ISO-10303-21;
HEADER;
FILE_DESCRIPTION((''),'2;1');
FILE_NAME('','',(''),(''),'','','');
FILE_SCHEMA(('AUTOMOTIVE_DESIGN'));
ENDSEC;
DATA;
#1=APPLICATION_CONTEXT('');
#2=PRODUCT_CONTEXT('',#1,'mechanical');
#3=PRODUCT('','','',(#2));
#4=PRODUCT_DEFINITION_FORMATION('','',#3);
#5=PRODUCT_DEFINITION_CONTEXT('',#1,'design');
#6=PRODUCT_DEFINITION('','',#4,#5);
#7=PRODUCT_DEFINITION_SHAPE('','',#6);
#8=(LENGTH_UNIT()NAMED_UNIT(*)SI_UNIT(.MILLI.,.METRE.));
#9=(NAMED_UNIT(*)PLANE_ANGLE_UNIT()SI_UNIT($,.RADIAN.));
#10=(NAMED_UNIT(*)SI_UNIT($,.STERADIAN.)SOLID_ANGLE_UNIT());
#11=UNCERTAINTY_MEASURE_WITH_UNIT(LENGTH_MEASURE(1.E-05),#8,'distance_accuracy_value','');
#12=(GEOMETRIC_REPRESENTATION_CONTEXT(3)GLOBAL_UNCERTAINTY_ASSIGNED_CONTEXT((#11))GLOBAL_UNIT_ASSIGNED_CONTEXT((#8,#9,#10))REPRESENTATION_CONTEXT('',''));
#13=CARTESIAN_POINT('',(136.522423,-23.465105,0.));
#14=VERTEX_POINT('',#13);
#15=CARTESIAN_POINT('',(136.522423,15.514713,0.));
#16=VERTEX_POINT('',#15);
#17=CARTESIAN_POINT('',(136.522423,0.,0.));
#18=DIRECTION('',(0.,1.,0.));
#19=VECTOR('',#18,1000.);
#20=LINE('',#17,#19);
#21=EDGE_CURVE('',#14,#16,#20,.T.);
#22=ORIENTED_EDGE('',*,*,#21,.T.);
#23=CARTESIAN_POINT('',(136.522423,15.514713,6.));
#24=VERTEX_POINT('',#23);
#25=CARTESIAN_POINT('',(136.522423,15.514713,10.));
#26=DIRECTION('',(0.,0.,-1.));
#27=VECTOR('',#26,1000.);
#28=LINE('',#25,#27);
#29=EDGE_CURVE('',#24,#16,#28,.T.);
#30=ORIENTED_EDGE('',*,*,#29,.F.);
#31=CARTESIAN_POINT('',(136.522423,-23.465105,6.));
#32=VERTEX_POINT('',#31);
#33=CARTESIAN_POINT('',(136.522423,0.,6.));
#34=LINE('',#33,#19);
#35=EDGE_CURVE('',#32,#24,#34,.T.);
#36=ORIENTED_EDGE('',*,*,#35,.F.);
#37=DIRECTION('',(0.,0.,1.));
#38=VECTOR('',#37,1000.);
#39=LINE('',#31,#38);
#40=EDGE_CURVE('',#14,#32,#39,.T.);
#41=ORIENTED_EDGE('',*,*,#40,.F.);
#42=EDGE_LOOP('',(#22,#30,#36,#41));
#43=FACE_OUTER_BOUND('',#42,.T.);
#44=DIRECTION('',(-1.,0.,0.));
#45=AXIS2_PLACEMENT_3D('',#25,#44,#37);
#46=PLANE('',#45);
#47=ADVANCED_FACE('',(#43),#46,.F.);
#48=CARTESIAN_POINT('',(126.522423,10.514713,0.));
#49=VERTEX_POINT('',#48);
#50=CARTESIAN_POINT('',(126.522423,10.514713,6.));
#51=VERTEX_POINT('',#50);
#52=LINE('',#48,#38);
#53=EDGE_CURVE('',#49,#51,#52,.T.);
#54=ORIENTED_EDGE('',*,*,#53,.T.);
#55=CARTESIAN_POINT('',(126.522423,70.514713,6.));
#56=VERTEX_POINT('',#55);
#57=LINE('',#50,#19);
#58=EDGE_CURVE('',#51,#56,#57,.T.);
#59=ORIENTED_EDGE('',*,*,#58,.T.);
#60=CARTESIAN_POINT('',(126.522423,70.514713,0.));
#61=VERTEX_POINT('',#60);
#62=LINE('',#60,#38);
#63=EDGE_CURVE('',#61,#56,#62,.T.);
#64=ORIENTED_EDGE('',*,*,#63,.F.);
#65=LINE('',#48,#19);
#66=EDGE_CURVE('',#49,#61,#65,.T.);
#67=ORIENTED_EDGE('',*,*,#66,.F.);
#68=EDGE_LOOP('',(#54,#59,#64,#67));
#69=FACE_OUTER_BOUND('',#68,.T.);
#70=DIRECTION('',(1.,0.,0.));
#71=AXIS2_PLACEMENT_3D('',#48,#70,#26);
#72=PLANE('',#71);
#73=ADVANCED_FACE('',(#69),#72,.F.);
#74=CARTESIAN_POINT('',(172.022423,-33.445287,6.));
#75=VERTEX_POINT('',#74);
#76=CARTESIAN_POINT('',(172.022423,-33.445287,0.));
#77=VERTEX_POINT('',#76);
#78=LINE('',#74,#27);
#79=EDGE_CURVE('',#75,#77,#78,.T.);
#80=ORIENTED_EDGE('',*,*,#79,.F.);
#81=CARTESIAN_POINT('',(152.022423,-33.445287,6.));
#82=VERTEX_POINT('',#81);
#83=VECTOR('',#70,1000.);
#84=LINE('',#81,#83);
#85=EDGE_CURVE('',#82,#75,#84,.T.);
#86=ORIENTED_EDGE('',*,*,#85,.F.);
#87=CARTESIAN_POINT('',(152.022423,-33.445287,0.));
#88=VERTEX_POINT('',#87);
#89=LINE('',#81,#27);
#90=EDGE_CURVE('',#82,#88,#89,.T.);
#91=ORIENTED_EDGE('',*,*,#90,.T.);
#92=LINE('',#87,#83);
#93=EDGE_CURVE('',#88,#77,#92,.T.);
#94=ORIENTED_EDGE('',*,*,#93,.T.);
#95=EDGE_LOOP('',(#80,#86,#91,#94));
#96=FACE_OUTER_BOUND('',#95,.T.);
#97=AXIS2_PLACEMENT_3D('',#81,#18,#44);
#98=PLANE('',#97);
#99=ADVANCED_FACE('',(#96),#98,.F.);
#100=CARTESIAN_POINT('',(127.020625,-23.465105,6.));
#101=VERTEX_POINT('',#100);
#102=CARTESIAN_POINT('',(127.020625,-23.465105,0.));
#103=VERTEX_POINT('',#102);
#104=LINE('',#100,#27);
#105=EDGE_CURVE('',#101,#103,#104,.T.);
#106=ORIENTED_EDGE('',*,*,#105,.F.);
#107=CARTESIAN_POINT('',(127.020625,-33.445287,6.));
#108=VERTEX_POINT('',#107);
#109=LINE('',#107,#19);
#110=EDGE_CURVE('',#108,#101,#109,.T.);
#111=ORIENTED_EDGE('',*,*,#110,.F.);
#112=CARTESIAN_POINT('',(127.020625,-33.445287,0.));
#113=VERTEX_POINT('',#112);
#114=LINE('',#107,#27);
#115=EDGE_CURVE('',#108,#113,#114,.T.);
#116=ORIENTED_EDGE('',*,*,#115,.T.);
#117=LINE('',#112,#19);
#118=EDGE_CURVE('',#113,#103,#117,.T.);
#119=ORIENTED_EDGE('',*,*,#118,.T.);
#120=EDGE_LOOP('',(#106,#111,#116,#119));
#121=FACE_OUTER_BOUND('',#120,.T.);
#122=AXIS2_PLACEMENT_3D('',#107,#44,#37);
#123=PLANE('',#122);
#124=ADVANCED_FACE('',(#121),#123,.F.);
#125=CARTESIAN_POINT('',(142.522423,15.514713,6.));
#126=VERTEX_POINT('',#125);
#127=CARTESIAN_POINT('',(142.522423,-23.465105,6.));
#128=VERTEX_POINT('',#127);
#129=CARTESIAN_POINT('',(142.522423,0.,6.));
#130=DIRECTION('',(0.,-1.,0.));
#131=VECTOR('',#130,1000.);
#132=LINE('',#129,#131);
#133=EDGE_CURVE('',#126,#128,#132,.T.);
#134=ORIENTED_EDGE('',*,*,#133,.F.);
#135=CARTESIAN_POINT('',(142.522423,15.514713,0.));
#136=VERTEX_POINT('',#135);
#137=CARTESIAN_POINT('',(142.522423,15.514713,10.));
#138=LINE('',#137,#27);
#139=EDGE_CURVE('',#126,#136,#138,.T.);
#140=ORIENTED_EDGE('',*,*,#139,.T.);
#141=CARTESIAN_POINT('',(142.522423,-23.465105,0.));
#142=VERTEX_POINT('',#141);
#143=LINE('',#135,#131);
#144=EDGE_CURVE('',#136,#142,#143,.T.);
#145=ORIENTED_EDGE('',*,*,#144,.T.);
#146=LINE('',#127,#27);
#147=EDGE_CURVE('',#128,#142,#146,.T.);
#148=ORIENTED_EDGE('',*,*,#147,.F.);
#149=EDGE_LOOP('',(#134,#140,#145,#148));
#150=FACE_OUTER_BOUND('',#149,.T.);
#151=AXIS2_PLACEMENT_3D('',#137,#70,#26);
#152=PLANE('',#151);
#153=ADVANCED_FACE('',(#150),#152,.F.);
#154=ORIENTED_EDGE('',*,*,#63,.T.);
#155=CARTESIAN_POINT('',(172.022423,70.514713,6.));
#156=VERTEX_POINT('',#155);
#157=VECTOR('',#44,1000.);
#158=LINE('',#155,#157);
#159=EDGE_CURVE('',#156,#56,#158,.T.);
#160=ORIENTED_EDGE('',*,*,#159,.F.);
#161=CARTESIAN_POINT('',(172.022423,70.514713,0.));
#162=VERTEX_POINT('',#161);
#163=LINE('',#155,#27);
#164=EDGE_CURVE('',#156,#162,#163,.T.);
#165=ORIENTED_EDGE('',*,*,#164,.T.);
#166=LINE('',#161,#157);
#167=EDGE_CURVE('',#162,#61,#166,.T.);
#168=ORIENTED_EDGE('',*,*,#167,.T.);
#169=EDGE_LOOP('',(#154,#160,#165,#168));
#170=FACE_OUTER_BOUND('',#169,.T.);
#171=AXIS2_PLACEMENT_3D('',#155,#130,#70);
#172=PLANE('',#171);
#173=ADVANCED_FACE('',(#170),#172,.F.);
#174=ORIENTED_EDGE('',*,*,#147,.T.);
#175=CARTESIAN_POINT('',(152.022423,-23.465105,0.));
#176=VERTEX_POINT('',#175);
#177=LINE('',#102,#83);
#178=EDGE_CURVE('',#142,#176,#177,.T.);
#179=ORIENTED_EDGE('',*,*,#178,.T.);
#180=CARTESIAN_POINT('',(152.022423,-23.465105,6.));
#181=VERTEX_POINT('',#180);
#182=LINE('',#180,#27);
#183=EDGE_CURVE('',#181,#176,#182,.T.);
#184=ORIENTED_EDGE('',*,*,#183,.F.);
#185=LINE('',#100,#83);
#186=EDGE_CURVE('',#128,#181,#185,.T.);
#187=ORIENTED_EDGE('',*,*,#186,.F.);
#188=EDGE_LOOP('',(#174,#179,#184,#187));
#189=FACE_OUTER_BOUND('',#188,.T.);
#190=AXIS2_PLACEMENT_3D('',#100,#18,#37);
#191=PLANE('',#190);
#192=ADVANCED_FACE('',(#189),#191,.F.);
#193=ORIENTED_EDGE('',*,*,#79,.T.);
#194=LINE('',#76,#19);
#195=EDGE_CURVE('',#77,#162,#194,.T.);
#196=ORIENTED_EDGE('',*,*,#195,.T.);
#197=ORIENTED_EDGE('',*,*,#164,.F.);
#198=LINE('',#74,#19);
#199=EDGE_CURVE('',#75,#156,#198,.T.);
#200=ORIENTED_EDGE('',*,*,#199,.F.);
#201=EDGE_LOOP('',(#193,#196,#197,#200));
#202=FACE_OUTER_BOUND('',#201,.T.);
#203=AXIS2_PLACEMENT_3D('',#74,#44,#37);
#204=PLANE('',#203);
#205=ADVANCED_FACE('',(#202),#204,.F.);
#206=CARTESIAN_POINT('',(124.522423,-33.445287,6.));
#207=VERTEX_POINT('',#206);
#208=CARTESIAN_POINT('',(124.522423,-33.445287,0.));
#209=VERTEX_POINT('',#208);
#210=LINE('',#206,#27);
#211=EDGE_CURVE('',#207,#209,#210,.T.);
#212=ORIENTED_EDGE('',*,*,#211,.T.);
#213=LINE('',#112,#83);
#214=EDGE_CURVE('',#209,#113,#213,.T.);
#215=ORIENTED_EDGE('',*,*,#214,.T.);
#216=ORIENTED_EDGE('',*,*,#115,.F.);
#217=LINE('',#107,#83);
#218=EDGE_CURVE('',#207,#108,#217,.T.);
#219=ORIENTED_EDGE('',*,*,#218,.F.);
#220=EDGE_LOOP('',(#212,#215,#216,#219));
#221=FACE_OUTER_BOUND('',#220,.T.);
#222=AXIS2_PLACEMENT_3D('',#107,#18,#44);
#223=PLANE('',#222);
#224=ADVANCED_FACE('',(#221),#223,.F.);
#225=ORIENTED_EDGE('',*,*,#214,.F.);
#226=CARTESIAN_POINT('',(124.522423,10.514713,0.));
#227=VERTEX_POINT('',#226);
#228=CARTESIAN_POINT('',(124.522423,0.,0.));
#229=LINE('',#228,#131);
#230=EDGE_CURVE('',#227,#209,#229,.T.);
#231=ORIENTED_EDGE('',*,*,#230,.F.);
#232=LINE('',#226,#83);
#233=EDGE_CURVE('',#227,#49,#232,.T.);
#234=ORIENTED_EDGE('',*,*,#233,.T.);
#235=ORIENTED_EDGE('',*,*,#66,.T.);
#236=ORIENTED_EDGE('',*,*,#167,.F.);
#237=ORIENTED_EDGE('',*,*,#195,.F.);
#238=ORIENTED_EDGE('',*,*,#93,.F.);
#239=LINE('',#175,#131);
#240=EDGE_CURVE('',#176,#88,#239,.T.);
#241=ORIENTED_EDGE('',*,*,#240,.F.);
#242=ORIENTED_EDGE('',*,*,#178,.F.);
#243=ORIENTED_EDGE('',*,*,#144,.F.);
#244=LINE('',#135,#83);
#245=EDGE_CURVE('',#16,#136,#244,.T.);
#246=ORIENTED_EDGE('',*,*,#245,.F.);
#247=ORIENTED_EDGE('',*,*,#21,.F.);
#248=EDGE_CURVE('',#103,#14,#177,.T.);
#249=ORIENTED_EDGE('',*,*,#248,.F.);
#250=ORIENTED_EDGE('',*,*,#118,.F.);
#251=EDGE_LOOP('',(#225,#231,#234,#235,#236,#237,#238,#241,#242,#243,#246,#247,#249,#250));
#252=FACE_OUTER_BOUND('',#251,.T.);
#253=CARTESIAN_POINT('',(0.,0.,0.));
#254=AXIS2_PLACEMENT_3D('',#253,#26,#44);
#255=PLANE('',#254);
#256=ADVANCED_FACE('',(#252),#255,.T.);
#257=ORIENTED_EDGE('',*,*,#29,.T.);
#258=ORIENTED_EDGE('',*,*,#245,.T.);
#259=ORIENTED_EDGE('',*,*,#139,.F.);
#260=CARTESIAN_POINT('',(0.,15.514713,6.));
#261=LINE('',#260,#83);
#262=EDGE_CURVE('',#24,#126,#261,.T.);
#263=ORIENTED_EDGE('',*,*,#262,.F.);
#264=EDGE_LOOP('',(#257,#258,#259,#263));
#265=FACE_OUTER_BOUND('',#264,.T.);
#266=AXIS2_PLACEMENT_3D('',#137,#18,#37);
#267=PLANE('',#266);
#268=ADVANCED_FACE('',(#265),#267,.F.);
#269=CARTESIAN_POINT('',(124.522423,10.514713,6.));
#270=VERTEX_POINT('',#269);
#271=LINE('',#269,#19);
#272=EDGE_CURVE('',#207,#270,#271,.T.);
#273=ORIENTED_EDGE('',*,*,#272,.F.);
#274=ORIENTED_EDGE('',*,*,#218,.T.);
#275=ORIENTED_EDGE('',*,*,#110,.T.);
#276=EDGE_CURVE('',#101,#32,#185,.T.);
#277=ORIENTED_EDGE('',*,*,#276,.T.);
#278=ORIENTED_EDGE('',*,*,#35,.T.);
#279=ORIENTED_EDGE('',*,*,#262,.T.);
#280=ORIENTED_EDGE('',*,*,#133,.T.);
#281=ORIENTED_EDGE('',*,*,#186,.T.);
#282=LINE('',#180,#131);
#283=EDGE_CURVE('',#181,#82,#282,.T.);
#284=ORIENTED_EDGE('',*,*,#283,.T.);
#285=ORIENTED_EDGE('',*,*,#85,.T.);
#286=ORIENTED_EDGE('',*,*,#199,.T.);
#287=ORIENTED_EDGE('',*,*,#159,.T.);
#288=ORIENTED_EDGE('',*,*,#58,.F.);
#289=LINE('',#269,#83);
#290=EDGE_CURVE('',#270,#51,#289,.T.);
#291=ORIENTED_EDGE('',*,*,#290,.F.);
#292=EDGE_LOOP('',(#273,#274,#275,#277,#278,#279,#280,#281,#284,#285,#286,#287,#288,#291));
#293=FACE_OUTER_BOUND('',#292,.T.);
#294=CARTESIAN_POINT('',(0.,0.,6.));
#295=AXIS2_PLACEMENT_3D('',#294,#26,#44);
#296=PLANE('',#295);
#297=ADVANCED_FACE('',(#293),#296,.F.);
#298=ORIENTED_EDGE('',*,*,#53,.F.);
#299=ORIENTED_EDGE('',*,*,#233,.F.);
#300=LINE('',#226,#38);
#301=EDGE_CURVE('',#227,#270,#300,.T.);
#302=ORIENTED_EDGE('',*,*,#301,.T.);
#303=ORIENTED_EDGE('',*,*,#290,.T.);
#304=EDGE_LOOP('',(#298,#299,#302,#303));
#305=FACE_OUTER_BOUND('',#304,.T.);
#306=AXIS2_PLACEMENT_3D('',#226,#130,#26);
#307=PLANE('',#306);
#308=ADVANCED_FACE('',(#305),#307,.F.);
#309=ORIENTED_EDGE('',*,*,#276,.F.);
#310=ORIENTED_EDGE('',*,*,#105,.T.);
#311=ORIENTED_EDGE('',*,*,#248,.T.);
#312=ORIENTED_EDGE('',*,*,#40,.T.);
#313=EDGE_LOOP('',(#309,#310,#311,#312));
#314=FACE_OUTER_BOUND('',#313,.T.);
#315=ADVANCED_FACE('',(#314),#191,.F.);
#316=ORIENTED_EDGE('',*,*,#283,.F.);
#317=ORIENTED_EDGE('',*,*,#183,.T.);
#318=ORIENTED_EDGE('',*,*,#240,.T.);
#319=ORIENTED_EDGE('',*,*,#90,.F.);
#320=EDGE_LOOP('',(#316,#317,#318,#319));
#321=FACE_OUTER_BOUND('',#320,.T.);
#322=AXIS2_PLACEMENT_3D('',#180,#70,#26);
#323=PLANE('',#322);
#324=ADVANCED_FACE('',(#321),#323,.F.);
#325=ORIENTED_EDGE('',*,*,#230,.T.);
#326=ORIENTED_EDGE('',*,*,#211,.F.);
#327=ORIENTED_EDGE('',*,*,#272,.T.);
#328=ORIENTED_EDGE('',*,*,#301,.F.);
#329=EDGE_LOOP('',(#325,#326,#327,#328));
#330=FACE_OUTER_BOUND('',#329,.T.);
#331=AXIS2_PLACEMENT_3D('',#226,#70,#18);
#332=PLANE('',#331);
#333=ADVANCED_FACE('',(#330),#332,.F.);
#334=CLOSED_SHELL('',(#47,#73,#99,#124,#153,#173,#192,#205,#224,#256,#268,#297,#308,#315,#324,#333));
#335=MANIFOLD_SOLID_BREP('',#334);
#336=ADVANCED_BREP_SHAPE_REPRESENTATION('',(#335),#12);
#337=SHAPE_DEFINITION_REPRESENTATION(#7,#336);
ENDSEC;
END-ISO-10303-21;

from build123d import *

# Parameters (mm, degrees)
BOSS_EXTRUDE1_DEPTH = 6
SKETCH3_W           = 6
SKETCH3_H           = 60
CUT_EXTRUDE1_DEPTH  = 10
CUT_EXTRUDE2_DEPTH  = 187.01085661


with BuildPart() as part:
    # Sketch1 → Boss-Extrude1 (new body)
    with BuildSketch(Plane.XY):
        Polygon((127.020625139, -33.445286794), (107.020625139, -33.445286794), (107.020625139, 70.514713206), (172.022422952, 70.514713206), (172.022422952, -33.445286794), (152.022422952, -33.445286794), (152.022422952, -23.465104548), (127.020625139, -23.465104548), align=None)
    extrude(amount=BOSS_EXTRUDE1_DEPTH)

    # Sketch3 → Cut-Extrude1 (cut)
    with BuildSketch(Plane(origin=(0, 0, 0), x_dir=(-1, 0, 0), z_dir=(0, 0, -1))):
        with Locations((-139.522422952, -14.485286794)):
            Rectangle(SKETCH3_W, SKETCH3_H)
    extrude(amount=-CUT_EXTRUDE1_DEPTH, mode=Mode.SUBTRACT)

    # Sketch4 → Cut-Extrude2 (cut, through all)
    with BuildSketch(Plane.XY.offset(6)):
        Polygon((124.522422952, -36.580409203), (107.020625139, -36.580409203), (107.020625139, 70.514713206), (120.512520278, 70.514713206), (126.522422952, 70.514713206), (126.522422952, 10.514713206), (124.522422952, 10.514713206), align=None)
    extrude(amount=-CUT_EXTRUDE2_DEPTH, mode=Mode.SUBTRACT)


solid = part.part
